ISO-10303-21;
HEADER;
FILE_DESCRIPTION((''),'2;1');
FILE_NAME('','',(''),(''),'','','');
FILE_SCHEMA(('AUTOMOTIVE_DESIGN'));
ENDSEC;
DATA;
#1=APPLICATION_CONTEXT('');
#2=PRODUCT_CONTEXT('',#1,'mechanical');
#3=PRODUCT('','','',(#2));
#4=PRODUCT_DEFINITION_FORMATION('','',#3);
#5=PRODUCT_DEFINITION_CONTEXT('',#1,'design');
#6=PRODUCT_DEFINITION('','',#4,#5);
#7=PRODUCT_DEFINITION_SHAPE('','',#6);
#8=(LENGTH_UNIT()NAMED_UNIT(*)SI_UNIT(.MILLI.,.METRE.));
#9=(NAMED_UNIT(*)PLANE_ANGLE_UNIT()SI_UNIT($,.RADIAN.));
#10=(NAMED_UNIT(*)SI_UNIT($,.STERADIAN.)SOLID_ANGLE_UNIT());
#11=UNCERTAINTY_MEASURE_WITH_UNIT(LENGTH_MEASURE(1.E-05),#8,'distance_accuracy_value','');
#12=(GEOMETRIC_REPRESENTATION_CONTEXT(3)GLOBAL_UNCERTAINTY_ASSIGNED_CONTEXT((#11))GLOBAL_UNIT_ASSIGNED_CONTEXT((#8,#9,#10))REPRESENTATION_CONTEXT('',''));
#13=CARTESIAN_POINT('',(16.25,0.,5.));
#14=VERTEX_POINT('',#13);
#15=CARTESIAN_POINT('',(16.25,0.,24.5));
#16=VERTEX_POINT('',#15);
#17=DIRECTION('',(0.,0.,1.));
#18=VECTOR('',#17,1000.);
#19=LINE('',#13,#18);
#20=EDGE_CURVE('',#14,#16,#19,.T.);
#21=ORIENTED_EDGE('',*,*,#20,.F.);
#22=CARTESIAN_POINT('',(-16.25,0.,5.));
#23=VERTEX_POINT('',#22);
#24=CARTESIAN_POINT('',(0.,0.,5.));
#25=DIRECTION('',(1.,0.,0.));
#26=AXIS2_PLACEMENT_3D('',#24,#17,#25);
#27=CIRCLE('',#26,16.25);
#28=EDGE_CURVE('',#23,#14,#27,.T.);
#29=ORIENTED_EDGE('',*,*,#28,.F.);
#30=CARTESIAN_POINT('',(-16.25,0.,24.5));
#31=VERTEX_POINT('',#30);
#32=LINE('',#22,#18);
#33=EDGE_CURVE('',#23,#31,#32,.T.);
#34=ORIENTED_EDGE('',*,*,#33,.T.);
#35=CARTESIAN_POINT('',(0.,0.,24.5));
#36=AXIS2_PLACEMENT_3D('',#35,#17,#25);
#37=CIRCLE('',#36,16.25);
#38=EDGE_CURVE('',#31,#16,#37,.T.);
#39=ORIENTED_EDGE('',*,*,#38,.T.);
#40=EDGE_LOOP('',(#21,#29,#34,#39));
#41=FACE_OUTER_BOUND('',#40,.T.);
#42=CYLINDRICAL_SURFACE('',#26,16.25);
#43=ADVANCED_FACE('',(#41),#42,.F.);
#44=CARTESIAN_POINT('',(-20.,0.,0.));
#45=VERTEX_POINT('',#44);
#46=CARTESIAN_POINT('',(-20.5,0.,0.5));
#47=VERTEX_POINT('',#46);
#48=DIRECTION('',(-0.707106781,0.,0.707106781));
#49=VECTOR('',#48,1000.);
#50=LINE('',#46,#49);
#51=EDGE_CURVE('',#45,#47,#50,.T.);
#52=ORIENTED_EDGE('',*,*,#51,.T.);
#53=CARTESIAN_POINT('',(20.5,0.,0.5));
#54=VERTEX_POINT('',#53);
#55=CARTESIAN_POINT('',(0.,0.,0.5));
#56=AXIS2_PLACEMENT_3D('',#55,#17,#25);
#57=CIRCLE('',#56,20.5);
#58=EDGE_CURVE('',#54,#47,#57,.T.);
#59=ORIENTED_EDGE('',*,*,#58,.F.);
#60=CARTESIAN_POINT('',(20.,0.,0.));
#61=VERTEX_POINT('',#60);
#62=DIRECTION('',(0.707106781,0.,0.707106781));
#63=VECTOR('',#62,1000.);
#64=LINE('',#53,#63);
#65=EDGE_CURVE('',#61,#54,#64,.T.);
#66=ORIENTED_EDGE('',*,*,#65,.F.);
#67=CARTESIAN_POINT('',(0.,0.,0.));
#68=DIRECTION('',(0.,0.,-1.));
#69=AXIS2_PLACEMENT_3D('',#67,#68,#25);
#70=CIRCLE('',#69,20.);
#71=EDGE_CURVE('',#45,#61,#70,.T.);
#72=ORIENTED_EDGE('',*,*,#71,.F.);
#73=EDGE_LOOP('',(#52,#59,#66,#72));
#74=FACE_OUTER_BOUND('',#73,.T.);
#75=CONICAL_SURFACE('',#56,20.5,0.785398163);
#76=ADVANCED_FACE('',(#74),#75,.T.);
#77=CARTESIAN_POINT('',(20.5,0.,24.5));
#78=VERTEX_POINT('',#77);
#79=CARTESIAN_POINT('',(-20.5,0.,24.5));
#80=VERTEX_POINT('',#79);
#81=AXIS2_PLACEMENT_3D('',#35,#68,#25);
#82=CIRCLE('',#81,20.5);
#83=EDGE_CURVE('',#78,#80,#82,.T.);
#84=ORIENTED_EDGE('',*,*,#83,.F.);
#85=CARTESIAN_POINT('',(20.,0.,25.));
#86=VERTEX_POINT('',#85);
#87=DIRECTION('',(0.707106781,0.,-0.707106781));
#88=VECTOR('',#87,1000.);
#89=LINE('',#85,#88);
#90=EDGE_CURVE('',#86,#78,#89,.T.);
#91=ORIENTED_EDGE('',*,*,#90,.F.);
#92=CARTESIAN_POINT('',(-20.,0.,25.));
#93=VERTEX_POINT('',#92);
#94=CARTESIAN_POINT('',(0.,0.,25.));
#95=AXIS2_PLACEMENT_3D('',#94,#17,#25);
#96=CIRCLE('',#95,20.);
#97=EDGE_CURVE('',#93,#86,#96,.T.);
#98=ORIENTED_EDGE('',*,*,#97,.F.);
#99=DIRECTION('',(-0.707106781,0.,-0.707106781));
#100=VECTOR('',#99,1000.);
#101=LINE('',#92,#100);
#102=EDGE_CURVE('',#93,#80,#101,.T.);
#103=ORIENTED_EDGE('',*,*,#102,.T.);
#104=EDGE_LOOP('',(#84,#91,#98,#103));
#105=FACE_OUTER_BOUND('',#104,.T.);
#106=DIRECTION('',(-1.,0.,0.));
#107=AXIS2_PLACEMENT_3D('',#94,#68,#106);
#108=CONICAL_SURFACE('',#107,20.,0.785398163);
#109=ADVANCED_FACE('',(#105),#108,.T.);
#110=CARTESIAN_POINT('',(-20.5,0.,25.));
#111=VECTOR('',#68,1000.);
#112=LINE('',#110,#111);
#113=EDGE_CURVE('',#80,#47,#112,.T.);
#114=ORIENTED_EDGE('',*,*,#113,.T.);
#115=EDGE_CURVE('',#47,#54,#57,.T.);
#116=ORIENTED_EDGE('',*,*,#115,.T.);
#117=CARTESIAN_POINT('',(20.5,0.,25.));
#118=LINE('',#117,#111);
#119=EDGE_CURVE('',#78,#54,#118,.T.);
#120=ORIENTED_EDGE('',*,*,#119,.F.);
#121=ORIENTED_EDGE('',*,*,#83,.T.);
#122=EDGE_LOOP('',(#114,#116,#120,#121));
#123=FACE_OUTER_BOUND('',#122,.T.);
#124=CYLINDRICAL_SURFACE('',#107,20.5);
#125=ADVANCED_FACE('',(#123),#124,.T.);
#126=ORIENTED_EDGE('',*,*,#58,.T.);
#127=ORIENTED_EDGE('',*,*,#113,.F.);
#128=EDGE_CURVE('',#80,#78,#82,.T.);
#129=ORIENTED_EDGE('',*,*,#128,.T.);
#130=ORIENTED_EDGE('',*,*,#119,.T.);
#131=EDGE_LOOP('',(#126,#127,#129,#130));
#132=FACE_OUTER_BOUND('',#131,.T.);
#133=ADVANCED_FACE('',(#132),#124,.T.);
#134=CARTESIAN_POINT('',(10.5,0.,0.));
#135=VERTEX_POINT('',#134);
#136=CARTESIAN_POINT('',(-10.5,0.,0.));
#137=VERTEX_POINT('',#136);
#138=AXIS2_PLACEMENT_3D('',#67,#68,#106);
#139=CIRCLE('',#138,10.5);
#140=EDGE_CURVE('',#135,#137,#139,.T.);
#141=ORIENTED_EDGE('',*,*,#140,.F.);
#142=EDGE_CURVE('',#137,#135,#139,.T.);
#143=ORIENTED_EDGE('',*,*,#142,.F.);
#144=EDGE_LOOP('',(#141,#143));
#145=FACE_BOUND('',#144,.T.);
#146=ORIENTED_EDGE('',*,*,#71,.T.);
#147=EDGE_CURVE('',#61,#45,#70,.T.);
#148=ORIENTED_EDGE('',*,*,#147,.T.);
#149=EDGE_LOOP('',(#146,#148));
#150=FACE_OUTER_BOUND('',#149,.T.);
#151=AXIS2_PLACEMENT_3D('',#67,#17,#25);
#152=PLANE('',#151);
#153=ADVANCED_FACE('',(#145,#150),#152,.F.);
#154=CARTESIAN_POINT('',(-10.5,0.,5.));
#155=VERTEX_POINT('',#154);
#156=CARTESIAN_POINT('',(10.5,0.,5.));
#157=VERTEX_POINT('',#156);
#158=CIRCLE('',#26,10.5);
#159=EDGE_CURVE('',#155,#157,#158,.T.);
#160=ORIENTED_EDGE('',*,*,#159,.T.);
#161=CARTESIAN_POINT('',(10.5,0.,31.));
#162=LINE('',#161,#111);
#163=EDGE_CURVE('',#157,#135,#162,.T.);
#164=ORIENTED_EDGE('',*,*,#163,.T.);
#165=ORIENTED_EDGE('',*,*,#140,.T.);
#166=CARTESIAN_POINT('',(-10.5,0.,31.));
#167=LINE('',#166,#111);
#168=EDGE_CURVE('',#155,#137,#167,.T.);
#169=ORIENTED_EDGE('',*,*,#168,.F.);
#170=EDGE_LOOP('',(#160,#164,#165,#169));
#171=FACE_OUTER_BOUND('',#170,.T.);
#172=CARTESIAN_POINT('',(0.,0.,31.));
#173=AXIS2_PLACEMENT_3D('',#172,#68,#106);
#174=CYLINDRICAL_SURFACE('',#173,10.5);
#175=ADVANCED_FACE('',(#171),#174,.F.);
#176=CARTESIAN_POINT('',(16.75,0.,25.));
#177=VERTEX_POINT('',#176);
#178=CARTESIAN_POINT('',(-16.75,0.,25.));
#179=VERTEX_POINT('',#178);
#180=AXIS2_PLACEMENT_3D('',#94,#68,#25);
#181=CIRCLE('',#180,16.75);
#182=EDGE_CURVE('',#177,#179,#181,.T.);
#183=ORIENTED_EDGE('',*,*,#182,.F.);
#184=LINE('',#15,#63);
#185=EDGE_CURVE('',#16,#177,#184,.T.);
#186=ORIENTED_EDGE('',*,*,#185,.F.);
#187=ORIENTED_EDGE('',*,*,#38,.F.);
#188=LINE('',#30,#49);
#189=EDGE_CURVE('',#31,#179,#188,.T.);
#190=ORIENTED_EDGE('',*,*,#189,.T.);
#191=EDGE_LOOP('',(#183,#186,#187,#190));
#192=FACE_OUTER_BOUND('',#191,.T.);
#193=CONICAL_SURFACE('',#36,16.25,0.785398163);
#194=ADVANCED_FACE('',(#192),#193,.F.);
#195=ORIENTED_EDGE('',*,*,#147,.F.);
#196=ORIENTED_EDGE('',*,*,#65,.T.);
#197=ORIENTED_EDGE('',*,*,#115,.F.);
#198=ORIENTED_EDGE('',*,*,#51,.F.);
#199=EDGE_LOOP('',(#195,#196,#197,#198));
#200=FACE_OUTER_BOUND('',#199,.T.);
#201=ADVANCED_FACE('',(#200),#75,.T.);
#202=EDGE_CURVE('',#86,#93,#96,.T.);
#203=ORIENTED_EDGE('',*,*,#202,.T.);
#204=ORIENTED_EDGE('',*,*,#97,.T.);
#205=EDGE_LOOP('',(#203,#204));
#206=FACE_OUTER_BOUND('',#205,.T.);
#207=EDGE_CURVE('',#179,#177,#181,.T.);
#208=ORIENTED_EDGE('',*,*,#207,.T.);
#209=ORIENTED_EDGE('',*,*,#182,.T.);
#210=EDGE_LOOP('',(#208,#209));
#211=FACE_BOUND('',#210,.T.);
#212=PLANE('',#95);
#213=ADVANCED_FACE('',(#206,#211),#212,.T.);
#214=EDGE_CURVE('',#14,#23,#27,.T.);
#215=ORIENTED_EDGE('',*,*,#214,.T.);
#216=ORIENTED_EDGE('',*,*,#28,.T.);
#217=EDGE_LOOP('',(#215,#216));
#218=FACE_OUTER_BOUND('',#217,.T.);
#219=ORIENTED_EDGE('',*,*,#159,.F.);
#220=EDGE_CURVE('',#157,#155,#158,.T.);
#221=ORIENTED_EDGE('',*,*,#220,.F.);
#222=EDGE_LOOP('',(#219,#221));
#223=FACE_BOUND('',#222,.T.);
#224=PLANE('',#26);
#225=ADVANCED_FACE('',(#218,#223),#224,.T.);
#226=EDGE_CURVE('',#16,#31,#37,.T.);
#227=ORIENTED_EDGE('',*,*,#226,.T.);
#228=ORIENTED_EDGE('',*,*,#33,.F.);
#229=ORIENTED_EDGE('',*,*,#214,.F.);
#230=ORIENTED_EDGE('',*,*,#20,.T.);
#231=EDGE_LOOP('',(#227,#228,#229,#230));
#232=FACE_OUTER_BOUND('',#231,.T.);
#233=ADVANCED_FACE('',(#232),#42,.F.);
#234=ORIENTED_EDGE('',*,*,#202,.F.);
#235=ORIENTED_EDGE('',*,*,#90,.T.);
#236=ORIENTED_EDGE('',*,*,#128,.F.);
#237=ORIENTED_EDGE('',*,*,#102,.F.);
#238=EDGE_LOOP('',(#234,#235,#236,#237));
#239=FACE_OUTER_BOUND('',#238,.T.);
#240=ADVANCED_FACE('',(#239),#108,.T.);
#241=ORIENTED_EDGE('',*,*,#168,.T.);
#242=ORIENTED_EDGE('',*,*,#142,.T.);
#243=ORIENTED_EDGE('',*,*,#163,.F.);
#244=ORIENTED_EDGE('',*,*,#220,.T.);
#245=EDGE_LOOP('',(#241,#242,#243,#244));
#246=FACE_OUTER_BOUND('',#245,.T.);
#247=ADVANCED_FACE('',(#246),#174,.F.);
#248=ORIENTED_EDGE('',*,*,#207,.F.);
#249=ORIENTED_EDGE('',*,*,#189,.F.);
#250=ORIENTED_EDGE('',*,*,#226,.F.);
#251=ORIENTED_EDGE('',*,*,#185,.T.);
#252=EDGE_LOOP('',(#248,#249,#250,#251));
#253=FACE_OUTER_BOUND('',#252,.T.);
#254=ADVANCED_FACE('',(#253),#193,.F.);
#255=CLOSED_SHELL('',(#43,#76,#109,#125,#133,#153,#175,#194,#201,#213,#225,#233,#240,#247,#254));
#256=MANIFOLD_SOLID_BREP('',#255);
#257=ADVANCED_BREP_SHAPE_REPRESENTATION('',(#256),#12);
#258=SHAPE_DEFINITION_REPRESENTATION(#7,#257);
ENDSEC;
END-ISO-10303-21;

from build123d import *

# Parameters (mm, degrees)
SKETCH1_R           = 20.5
BOSS_EXTRUDE1_DEPTH = 25
CHAMFER1_SIZE       = 0.5
SKETCH5_R           = 16.25
CUT_EXTRUDE1_DEPTH  = 20
CHAMFER2_SIZE       = 0.5
SKETCH6_R           = 10.5
CUT_EXTRUDE2_DEPTH  = 31


with BuildPart() as part:
    # Sketch1 → Boss-Extrude1 (new body)
    with BuildSketch(Plane.XY):
        Circle(SKETCH1_R)
    extrude(amount=BOSS_EXTRUDE1_DEPTH)

    # Chamfer1
    chamfer1_edges = [part.edges().sort_by_distance(p)[0] for p in [
        (-20.5, 0, 0),
        (-20.5, 0, 25),
    ]]
    chamfer(chamfer1_edges, length=CHAMFER1_SIZE)

    # Sketch5 → Cut-Extrude1 (cut)
    with BuildSketch(Plane.XY.offset(25)):
        Circle(SKETCH5_R)
    extrude(amount=-CUT_EXTRUDE1_DEPTH, mode=Mode.SUBTRACT)

    # Chamfer2
    chamfer2_edges = [part.edges().sort_by_distance(p)[0] for p in [
        (-16.25, 0, 25),
    ]]
    chamfer(chamfer2_edges, length=CHAMFER2_SIZE)

    # Sketch6 → Cut-Extrude2 (cut)
    with BuildSketch(Plane(origin=(0, 0, 0), x_dir=(-1, 0, 0), z_dir=(0, 0, -1))):
        Circle(SKETCH6_R)
    extrude(amount=-CUT_EXTRUDE2_DEPTH, mode=Mode.SUBTRACT)


solid = part.part
